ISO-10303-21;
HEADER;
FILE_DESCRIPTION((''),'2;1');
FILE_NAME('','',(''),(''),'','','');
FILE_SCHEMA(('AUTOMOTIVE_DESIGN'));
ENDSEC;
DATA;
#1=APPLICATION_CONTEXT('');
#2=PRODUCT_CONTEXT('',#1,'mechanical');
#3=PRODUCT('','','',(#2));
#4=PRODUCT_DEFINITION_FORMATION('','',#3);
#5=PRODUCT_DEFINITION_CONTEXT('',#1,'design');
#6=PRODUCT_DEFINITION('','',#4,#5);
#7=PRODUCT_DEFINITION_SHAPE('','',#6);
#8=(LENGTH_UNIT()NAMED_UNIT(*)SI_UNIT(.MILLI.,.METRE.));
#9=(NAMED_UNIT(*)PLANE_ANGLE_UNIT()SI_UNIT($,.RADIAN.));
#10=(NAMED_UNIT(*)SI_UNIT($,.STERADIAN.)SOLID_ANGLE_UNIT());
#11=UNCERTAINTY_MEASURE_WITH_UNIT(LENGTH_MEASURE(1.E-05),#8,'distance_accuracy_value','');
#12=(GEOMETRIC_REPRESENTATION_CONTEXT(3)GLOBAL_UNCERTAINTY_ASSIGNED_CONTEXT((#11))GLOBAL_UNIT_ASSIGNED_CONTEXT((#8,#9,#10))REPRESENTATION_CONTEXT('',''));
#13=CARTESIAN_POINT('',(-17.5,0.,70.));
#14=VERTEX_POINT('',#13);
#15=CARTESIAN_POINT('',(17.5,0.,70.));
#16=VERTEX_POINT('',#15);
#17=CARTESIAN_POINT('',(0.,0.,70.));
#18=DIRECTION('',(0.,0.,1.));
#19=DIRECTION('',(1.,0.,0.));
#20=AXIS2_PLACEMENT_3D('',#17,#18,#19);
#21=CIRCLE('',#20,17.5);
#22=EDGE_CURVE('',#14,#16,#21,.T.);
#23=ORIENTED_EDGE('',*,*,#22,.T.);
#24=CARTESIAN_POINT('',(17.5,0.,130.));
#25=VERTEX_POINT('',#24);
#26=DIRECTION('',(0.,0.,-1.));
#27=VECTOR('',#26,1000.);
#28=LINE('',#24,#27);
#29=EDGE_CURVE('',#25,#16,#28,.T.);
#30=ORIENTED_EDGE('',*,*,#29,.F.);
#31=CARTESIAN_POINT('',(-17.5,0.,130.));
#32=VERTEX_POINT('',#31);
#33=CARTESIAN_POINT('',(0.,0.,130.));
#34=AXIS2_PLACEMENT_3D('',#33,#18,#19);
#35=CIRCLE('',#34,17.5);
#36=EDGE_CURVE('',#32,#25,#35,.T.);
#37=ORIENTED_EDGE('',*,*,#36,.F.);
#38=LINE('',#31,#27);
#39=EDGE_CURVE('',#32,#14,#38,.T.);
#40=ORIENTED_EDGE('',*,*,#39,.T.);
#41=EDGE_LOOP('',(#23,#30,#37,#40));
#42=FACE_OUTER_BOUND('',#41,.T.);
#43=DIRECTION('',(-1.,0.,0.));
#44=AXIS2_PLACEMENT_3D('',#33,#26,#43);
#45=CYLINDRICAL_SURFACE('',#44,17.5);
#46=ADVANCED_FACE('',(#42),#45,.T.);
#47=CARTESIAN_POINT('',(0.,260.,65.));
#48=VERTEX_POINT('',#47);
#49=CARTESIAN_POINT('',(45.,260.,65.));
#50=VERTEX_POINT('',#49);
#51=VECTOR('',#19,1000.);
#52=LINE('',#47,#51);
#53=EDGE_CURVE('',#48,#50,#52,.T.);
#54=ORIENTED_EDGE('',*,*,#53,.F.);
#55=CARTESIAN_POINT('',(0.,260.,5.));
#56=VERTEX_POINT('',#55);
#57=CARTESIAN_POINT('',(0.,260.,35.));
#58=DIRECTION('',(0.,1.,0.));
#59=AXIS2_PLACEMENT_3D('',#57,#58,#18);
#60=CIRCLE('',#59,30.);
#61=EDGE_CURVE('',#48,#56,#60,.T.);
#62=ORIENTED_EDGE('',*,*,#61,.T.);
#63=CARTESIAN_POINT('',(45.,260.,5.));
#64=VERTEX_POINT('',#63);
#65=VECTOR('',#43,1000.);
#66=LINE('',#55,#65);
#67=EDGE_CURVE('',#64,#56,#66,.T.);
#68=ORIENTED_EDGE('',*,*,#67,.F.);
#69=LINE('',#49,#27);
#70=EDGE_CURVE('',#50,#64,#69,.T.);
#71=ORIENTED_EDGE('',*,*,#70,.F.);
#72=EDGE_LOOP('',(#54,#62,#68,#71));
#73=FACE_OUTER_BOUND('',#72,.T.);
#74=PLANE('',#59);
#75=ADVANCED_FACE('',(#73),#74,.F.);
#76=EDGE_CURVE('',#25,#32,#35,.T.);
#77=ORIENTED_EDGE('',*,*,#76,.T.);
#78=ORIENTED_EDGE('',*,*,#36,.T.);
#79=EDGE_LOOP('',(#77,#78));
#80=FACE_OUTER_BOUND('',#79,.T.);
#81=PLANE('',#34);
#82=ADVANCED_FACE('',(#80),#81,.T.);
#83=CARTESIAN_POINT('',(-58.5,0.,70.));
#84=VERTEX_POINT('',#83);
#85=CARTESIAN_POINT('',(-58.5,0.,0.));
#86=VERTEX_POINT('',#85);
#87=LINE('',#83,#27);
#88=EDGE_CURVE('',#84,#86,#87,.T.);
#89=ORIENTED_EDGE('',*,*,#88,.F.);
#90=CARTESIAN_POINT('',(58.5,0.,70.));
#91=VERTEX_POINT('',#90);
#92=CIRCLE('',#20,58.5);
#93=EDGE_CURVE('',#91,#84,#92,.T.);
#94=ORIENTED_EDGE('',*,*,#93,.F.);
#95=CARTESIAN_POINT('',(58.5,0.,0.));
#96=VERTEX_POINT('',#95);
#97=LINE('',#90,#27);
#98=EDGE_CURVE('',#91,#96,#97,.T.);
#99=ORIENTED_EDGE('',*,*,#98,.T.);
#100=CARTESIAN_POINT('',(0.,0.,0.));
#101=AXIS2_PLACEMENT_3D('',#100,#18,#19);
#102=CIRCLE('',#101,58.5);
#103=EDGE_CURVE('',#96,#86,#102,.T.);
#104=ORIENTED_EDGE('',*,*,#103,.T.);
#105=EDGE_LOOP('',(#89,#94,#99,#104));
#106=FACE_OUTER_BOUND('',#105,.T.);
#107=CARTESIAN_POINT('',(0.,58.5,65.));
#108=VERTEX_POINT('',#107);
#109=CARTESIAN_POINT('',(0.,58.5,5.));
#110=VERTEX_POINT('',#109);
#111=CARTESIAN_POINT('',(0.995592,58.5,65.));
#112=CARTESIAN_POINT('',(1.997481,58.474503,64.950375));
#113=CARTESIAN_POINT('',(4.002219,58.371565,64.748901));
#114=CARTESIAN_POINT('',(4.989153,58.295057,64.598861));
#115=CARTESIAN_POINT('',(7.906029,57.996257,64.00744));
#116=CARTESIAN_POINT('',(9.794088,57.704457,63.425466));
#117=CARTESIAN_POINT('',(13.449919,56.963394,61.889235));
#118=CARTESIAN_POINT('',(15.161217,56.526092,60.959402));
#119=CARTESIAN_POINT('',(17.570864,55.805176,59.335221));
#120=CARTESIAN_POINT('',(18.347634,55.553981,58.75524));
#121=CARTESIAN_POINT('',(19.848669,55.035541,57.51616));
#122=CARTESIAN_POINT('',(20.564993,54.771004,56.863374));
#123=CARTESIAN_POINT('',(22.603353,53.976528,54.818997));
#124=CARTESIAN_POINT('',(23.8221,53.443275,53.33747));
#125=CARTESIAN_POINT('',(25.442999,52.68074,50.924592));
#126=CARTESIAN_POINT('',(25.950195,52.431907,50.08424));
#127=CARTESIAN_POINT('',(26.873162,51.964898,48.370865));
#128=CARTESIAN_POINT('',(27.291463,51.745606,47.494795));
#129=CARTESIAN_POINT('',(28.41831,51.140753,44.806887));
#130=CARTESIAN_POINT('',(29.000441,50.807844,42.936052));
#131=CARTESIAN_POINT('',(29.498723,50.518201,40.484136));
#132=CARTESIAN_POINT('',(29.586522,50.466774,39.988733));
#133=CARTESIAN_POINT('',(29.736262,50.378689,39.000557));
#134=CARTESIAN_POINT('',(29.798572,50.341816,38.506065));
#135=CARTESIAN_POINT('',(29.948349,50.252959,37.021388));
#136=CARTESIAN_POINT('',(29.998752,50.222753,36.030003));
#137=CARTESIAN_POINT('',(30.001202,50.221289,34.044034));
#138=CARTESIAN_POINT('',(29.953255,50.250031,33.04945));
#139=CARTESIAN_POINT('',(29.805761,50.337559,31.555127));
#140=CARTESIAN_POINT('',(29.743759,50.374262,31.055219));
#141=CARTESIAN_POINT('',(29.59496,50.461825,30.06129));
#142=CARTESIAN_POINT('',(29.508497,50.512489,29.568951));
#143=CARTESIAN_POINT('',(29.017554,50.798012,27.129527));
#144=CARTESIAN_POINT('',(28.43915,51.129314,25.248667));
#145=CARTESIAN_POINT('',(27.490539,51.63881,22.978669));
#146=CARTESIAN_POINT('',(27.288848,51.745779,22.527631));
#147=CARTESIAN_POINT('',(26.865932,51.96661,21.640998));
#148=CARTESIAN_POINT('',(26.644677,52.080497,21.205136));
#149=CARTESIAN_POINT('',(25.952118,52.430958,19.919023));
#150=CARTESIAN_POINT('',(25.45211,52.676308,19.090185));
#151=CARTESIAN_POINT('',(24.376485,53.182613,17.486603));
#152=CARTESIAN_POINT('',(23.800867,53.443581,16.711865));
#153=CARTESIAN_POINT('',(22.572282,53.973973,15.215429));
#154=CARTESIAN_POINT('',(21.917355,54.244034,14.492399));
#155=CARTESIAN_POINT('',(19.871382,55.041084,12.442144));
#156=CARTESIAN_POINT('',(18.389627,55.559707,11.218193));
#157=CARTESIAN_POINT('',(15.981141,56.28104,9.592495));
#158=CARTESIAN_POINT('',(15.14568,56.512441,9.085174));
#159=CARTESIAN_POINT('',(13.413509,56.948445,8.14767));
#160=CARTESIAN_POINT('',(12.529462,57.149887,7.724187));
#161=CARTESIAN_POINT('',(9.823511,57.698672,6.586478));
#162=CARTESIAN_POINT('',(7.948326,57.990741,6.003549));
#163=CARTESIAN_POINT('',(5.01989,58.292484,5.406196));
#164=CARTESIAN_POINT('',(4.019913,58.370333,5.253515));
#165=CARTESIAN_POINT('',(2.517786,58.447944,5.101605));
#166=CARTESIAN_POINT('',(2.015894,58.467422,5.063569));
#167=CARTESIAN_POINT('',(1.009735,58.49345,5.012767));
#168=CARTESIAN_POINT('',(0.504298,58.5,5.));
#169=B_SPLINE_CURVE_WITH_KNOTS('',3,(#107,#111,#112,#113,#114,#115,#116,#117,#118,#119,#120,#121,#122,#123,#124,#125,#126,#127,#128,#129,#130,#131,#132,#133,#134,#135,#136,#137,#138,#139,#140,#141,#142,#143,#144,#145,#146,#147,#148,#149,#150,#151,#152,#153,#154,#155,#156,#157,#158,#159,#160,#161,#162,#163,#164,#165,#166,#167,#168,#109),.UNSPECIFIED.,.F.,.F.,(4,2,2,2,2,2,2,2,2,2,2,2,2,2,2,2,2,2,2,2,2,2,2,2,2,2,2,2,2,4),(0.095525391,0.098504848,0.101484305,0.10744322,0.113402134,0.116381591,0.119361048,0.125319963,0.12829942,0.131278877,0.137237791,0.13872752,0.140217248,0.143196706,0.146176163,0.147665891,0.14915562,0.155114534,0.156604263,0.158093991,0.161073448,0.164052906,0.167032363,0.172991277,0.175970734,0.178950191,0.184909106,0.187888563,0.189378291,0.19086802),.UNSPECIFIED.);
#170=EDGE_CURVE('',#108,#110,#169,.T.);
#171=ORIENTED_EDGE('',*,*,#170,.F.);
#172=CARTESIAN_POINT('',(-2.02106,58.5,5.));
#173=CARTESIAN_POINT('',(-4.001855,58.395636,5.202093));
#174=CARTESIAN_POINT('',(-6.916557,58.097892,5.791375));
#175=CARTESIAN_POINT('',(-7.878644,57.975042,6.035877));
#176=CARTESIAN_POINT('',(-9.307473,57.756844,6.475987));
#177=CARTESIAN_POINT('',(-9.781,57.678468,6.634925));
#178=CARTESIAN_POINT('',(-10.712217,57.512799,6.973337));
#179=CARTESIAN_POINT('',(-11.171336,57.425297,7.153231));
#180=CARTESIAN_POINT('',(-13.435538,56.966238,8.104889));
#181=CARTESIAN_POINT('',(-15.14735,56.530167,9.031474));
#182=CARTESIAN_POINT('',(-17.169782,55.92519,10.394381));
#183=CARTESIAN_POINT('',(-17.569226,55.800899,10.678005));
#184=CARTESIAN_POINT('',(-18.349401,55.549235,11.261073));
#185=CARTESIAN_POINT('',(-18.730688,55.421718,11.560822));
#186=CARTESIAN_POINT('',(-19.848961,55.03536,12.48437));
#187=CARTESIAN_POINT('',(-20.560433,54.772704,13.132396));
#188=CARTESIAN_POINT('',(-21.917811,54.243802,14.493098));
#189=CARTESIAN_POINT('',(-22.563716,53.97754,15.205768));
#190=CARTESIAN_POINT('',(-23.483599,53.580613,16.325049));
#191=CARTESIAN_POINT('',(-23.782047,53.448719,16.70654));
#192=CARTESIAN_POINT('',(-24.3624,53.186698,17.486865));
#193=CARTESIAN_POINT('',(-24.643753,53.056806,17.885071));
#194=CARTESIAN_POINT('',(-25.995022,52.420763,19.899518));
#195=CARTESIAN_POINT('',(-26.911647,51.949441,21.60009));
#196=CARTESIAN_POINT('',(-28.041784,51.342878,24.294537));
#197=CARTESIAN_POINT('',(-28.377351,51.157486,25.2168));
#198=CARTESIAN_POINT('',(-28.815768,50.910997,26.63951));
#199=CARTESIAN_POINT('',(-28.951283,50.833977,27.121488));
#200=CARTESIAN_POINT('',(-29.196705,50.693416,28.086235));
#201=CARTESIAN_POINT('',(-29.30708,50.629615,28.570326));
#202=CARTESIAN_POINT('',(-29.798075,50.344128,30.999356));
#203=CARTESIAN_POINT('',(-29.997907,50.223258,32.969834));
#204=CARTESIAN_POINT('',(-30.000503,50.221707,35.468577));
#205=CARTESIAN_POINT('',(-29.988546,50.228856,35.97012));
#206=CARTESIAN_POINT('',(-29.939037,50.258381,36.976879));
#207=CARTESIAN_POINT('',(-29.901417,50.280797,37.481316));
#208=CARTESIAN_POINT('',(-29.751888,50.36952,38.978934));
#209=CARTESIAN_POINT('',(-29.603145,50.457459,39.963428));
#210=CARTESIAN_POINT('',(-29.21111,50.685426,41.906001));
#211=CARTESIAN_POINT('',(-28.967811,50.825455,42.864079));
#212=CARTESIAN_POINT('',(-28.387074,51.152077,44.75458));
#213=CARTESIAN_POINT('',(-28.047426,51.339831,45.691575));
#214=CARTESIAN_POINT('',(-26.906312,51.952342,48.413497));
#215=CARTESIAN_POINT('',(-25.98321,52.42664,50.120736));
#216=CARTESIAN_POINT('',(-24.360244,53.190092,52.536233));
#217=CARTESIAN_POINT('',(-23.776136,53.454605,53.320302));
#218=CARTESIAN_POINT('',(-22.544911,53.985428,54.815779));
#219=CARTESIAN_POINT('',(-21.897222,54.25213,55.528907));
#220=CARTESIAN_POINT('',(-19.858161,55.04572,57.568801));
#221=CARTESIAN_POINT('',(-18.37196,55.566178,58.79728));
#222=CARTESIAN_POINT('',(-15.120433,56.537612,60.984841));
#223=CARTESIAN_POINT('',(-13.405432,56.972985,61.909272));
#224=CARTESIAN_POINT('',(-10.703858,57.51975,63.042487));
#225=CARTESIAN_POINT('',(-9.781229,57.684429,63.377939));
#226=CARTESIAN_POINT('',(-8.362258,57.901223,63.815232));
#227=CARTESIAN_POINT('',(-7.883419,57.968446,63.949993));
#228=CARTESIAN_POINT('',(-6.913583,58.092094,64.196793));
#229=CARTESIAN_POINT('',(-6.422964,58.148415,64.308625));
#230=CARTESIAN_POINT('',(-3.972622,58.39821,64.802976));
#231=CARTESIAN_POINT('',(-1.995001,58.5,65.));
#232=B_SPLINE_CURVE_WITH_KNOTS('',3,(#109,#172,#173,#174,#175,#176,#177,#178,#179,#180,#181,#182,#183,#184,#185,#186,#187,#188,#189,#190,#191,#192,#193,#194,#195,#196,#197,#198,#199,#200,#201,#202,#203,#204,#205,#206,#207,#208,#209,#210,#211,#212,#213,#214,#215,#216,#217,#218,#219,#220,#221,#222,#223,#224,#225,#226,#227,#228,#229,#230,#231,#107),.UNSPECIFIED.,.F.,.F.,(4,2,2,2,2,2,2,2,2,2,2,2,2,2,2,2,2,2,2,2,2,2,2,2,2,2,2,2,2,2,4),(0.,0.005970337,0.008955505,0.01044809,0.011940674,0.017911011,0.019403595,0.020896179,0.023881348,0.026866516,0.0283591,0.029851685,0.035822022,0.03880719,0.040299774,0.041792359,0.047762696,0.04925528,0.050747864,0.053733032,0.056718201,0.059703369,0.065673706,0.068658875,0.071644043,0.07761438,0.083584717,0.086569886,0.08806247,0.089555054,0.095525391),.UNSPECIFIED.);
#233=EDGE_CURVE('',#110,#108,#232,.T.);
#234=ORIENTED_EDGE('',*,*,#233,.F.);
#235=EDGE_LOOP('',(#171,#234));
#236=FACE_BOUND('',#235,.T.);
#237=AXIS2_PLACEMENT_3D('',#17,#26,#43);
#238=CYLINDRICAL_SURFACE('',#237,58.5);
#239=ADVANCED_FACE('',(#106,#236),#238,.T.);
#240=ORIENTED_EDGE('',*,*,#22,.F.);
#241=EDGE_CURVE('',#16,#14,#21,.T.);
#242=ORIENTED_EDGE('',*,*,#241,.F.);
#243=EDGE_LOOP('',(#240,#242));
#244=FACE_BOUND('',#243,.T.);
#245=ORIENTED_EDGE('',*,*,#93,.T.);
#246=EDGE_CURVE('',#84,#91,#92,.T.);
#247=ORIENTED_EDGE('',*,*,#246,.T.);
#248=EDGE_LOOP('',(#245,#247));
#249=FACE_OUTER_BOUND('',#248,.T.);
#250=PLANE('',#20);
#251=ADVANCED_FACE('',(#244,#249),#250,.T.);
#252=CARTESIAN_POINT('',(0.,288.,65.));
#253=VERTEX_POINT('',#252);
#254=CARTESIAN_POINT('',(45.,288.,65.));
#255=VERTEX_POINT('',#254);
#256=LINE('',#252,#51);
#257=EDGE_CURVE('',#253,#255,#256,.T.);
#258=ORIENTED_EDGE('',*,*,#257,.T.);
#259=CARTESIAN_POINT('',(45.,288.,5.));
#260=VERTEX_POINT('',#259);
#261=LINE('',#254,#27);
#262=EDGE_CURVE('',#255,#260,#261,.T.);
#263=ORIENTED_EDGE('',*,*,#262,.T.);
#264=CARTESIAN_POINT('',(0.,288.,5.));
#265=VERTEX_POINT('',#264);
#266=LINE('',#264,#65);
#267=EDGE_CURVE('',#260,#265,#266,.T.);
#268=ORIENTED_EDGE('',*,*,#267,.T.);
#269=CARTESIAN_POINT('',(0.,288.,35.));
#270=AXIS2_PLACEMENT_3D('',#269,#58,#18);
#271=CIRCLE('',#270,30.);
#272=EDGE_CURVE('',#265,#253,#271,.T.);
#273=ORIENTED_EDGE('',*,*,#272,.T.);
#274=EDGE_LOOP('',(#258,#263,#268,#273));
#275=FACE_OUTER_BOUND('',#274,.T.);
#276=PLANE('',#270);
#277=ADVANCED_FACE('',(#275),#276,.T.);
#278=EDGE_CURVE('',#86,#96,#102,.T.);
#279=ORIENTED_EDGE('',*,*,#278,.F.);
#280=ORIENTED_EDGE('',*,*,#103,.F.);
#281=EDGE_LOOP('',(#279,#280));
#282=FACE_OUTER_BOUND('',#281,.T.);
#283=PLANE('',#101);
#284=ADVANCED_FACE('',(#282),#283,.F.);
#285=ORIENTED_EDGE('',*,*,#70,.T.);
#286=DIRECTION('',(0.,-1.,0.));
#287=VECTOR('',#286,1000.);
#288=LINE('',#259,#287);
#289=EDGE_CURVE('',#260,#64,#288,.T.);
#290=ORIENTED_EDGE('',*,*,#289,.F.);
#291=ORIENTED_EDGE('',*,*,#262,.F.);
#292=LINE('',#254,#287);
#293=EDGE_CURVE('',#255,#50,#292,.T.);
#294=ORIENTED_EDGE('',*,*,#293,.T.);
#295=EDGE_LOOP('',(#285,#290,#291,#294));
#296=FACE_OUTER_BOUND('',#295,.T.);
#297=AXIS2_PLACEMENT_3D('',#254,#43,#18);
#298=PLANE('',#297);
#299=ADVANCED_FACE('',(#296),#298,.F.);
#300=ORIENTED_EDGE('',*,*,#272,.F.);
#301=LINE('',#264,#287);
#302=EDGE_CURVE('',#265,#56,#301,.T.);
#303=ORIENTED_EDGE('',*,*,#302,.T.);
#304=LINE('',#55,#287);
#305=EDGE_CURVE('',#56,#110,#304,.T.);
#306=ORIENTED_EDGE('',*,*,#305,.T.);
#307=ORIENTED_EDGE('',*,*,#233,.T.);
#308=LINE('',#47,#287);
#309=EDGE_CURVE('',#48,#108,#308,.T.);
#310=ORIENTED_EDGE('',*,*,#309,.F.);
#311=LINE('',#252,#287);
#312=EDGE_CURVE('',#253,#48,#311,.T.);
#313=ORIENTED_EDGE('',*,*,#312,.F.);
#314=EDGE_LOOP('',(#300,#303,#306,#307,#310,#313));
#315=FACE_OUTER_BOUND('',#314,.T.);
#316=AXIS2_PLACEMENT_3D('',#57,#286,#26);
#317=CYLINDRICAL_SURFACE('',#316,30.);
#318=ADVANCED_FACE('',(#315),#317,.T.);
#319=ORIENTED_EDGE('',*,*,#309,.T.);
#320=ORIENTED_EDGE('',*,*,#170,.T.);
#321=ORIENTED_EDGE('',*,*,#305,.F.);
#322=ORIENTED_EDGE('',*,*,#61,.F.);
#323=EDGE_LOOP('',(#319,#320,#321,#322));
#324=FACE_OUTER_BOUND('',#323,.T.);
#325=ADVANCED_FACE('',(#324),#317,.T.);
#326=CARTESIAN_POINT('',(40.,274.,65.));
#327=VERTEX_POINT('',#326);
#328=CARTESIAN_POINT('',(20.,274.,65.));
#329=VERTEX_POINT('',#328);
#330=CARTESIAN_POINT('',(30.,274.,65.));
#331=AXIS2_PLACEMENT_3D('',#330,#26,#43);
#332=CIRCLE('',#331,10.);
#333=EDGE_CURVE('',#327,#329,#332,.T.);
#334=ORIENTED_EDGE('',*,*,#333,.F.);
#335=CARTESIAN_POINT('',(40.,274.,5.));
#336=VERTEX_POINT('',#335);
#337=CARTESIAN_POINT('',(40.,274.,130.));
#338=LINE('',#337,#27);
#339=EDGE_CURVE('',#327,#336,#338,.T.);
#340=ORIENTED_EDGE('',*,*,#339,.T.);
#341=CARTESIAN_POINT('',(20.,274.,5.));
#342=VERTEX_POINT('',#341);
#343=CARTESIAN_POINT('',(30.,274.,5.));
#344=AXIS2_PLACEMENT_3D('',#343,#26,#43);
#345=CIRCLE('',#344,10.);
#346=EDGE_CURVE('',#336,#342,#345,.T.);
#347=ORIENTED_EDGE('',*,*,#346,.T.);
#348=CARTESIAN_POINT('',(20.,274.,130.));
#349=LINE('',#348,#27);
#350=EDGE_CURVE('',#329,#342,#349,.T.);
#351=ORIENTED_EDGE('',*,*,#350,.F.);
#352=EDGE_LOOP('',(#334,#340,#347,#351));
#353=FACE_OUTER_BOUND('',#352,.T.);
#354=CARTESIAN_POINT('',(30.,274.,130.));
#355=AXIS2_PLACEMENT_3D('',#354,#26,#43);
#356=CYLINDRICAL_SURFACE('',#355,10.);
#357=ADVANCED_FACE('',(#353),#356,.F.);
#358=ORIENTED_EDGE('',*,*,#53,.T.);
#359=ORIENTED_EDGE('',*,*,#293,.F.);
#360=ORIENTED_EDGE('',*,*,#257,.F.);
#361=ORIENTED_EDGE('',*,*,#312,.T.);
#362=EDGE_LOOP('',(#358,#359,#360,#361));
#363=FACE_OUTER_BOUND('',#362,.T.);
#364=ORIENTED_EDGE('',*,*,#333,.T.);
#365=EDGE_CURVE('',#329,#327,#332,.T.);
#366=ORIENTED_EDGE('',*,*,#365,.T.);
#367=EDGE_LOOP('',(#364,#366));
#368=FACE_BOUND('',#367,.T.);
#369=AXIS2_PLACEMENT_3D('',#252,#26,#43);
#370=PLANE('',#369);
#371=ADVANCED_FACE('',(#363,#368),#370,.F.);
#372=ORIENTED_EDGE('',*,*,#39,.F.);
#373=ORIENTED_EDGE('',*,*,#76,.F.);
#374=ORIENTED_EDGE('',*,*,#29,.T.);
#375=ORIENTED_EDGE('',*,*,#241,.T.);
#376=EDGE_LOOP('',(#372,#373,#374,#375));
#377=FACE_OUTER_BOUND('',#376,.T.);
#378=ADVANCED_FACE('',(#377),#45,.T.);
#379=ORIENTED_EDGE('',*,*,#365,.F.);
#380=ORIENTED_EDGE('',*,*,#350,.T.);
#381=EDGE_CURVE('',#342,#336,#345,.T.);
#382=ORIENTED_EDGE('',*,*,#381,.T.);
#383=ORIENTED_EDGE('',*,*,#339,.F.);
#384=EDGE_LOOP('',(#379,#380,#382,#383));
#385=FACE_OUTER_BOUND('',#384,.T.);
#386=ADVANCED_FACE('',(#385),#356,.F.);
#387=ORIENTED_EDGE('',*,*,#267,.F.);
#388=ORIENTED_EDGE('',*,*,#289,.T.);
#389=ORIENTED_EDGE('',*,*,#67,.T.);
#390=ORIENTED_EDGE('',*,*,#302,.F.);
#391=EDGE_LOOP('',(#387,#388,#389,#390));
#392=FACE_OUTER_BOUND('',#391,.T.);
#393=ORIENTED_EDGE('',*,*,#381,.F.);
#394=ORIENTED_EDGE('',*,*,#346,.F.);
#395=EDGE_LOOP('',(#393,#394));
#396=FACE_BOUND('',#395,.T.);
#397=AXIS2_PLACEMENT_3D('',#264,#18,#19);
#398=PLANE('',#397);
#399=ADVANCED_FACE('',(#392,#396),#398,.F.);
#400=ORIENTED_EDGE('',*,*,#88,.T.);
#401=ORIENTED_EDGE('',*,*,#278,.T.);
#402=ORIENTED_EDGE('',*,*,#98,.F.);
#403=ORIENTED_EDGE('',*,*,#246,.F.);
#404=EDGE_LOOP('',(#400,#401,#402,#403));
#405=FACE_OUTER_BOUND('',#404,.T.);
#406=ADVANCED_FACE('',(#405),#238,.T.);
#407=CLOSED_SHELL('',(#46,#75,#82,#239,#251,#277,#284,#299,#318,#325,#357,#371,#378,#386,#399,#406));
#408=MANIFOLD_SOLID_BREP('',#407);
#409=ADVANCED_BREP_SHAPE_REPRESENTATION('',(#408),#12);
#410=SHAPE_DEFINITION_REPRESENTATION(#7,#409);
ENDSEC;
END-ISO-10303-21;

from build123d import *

# Parameters (mm, degrees)
SKETCH1_R           = 58.5
BOSS_EXTRUDE1_DEPTH = 70
SKETCH2_R           = 30
BOSS_EXTRUDE2_DEPTH = 260
BOSS_EXTRUDE4_DEPTH = 28
SKETCH7_R           = 17.5
BOSS_EXTRUDE6_DEPTH = 60
SKETCH8_R           = 10
CUT_EXTRUDE1_DEPTH  = 320.360689612


with BuildPart() as part:
    # Sketch1 → Boss-Extrude1 (new body)
    with BuildSketch(Plane.XY):
        Circle(SKETCH1_R)
    extrude(amount=BOSS_EXTRUDE1_DEPTH)

    # Sketch2 → Boss-Extrude2 (add)
    with BuildSketch(Plane(origin=(0, 0, 0), x_dir=(1, 0, 0), z_dir=(0, 1, 0))):
        with Locations(Location((0, -35, 0), (0, 0, 90))):
            Circle(SKETCH2_R)
    extrude(amount=BOSS_EXTRUDE2_DEPTH)

    # Sketch4 → Boss-Extrude4 (add)
    with BuildSketch(Plane(origin=(0, 260, 0), x_dir=(1, 0, 0), z_dir=(0, 1, 0))):
        with BuildLine():
            Line((0, -65), (45, -65))
            Line((45, -65), (45, -5))
            Line((45, -5), (0, -5))
            ThreePointArc((0, -5), (-30, -35), (0, -65))
        make_face()
    extrude(amount=BOSS_EXTRUDE4_DEPTH)

    # Sketch7 → Boss-Extrude6 (add)
    with BuildSketch(Plane.XY.offset(70)):
        Circle(SKETCH7_R)
    extrude(amount=BOSS_EXTRUDE6_DEPTH)

    # Sketch8 → Cut-Extrude1 (cut, through all)
    with BuildSketch(Plane(origin=(0, 0, 5), x_dir=(-1, 0, 0), z_dir=(0, 0, -1))):
        with Locations((-30, 274)):
            Circle(SKETCH8_R)
    extrude(amount=-CUT_EXTRUDE1_DEPTH, mode=Mode.SUBTRACT)


solid = part.part
